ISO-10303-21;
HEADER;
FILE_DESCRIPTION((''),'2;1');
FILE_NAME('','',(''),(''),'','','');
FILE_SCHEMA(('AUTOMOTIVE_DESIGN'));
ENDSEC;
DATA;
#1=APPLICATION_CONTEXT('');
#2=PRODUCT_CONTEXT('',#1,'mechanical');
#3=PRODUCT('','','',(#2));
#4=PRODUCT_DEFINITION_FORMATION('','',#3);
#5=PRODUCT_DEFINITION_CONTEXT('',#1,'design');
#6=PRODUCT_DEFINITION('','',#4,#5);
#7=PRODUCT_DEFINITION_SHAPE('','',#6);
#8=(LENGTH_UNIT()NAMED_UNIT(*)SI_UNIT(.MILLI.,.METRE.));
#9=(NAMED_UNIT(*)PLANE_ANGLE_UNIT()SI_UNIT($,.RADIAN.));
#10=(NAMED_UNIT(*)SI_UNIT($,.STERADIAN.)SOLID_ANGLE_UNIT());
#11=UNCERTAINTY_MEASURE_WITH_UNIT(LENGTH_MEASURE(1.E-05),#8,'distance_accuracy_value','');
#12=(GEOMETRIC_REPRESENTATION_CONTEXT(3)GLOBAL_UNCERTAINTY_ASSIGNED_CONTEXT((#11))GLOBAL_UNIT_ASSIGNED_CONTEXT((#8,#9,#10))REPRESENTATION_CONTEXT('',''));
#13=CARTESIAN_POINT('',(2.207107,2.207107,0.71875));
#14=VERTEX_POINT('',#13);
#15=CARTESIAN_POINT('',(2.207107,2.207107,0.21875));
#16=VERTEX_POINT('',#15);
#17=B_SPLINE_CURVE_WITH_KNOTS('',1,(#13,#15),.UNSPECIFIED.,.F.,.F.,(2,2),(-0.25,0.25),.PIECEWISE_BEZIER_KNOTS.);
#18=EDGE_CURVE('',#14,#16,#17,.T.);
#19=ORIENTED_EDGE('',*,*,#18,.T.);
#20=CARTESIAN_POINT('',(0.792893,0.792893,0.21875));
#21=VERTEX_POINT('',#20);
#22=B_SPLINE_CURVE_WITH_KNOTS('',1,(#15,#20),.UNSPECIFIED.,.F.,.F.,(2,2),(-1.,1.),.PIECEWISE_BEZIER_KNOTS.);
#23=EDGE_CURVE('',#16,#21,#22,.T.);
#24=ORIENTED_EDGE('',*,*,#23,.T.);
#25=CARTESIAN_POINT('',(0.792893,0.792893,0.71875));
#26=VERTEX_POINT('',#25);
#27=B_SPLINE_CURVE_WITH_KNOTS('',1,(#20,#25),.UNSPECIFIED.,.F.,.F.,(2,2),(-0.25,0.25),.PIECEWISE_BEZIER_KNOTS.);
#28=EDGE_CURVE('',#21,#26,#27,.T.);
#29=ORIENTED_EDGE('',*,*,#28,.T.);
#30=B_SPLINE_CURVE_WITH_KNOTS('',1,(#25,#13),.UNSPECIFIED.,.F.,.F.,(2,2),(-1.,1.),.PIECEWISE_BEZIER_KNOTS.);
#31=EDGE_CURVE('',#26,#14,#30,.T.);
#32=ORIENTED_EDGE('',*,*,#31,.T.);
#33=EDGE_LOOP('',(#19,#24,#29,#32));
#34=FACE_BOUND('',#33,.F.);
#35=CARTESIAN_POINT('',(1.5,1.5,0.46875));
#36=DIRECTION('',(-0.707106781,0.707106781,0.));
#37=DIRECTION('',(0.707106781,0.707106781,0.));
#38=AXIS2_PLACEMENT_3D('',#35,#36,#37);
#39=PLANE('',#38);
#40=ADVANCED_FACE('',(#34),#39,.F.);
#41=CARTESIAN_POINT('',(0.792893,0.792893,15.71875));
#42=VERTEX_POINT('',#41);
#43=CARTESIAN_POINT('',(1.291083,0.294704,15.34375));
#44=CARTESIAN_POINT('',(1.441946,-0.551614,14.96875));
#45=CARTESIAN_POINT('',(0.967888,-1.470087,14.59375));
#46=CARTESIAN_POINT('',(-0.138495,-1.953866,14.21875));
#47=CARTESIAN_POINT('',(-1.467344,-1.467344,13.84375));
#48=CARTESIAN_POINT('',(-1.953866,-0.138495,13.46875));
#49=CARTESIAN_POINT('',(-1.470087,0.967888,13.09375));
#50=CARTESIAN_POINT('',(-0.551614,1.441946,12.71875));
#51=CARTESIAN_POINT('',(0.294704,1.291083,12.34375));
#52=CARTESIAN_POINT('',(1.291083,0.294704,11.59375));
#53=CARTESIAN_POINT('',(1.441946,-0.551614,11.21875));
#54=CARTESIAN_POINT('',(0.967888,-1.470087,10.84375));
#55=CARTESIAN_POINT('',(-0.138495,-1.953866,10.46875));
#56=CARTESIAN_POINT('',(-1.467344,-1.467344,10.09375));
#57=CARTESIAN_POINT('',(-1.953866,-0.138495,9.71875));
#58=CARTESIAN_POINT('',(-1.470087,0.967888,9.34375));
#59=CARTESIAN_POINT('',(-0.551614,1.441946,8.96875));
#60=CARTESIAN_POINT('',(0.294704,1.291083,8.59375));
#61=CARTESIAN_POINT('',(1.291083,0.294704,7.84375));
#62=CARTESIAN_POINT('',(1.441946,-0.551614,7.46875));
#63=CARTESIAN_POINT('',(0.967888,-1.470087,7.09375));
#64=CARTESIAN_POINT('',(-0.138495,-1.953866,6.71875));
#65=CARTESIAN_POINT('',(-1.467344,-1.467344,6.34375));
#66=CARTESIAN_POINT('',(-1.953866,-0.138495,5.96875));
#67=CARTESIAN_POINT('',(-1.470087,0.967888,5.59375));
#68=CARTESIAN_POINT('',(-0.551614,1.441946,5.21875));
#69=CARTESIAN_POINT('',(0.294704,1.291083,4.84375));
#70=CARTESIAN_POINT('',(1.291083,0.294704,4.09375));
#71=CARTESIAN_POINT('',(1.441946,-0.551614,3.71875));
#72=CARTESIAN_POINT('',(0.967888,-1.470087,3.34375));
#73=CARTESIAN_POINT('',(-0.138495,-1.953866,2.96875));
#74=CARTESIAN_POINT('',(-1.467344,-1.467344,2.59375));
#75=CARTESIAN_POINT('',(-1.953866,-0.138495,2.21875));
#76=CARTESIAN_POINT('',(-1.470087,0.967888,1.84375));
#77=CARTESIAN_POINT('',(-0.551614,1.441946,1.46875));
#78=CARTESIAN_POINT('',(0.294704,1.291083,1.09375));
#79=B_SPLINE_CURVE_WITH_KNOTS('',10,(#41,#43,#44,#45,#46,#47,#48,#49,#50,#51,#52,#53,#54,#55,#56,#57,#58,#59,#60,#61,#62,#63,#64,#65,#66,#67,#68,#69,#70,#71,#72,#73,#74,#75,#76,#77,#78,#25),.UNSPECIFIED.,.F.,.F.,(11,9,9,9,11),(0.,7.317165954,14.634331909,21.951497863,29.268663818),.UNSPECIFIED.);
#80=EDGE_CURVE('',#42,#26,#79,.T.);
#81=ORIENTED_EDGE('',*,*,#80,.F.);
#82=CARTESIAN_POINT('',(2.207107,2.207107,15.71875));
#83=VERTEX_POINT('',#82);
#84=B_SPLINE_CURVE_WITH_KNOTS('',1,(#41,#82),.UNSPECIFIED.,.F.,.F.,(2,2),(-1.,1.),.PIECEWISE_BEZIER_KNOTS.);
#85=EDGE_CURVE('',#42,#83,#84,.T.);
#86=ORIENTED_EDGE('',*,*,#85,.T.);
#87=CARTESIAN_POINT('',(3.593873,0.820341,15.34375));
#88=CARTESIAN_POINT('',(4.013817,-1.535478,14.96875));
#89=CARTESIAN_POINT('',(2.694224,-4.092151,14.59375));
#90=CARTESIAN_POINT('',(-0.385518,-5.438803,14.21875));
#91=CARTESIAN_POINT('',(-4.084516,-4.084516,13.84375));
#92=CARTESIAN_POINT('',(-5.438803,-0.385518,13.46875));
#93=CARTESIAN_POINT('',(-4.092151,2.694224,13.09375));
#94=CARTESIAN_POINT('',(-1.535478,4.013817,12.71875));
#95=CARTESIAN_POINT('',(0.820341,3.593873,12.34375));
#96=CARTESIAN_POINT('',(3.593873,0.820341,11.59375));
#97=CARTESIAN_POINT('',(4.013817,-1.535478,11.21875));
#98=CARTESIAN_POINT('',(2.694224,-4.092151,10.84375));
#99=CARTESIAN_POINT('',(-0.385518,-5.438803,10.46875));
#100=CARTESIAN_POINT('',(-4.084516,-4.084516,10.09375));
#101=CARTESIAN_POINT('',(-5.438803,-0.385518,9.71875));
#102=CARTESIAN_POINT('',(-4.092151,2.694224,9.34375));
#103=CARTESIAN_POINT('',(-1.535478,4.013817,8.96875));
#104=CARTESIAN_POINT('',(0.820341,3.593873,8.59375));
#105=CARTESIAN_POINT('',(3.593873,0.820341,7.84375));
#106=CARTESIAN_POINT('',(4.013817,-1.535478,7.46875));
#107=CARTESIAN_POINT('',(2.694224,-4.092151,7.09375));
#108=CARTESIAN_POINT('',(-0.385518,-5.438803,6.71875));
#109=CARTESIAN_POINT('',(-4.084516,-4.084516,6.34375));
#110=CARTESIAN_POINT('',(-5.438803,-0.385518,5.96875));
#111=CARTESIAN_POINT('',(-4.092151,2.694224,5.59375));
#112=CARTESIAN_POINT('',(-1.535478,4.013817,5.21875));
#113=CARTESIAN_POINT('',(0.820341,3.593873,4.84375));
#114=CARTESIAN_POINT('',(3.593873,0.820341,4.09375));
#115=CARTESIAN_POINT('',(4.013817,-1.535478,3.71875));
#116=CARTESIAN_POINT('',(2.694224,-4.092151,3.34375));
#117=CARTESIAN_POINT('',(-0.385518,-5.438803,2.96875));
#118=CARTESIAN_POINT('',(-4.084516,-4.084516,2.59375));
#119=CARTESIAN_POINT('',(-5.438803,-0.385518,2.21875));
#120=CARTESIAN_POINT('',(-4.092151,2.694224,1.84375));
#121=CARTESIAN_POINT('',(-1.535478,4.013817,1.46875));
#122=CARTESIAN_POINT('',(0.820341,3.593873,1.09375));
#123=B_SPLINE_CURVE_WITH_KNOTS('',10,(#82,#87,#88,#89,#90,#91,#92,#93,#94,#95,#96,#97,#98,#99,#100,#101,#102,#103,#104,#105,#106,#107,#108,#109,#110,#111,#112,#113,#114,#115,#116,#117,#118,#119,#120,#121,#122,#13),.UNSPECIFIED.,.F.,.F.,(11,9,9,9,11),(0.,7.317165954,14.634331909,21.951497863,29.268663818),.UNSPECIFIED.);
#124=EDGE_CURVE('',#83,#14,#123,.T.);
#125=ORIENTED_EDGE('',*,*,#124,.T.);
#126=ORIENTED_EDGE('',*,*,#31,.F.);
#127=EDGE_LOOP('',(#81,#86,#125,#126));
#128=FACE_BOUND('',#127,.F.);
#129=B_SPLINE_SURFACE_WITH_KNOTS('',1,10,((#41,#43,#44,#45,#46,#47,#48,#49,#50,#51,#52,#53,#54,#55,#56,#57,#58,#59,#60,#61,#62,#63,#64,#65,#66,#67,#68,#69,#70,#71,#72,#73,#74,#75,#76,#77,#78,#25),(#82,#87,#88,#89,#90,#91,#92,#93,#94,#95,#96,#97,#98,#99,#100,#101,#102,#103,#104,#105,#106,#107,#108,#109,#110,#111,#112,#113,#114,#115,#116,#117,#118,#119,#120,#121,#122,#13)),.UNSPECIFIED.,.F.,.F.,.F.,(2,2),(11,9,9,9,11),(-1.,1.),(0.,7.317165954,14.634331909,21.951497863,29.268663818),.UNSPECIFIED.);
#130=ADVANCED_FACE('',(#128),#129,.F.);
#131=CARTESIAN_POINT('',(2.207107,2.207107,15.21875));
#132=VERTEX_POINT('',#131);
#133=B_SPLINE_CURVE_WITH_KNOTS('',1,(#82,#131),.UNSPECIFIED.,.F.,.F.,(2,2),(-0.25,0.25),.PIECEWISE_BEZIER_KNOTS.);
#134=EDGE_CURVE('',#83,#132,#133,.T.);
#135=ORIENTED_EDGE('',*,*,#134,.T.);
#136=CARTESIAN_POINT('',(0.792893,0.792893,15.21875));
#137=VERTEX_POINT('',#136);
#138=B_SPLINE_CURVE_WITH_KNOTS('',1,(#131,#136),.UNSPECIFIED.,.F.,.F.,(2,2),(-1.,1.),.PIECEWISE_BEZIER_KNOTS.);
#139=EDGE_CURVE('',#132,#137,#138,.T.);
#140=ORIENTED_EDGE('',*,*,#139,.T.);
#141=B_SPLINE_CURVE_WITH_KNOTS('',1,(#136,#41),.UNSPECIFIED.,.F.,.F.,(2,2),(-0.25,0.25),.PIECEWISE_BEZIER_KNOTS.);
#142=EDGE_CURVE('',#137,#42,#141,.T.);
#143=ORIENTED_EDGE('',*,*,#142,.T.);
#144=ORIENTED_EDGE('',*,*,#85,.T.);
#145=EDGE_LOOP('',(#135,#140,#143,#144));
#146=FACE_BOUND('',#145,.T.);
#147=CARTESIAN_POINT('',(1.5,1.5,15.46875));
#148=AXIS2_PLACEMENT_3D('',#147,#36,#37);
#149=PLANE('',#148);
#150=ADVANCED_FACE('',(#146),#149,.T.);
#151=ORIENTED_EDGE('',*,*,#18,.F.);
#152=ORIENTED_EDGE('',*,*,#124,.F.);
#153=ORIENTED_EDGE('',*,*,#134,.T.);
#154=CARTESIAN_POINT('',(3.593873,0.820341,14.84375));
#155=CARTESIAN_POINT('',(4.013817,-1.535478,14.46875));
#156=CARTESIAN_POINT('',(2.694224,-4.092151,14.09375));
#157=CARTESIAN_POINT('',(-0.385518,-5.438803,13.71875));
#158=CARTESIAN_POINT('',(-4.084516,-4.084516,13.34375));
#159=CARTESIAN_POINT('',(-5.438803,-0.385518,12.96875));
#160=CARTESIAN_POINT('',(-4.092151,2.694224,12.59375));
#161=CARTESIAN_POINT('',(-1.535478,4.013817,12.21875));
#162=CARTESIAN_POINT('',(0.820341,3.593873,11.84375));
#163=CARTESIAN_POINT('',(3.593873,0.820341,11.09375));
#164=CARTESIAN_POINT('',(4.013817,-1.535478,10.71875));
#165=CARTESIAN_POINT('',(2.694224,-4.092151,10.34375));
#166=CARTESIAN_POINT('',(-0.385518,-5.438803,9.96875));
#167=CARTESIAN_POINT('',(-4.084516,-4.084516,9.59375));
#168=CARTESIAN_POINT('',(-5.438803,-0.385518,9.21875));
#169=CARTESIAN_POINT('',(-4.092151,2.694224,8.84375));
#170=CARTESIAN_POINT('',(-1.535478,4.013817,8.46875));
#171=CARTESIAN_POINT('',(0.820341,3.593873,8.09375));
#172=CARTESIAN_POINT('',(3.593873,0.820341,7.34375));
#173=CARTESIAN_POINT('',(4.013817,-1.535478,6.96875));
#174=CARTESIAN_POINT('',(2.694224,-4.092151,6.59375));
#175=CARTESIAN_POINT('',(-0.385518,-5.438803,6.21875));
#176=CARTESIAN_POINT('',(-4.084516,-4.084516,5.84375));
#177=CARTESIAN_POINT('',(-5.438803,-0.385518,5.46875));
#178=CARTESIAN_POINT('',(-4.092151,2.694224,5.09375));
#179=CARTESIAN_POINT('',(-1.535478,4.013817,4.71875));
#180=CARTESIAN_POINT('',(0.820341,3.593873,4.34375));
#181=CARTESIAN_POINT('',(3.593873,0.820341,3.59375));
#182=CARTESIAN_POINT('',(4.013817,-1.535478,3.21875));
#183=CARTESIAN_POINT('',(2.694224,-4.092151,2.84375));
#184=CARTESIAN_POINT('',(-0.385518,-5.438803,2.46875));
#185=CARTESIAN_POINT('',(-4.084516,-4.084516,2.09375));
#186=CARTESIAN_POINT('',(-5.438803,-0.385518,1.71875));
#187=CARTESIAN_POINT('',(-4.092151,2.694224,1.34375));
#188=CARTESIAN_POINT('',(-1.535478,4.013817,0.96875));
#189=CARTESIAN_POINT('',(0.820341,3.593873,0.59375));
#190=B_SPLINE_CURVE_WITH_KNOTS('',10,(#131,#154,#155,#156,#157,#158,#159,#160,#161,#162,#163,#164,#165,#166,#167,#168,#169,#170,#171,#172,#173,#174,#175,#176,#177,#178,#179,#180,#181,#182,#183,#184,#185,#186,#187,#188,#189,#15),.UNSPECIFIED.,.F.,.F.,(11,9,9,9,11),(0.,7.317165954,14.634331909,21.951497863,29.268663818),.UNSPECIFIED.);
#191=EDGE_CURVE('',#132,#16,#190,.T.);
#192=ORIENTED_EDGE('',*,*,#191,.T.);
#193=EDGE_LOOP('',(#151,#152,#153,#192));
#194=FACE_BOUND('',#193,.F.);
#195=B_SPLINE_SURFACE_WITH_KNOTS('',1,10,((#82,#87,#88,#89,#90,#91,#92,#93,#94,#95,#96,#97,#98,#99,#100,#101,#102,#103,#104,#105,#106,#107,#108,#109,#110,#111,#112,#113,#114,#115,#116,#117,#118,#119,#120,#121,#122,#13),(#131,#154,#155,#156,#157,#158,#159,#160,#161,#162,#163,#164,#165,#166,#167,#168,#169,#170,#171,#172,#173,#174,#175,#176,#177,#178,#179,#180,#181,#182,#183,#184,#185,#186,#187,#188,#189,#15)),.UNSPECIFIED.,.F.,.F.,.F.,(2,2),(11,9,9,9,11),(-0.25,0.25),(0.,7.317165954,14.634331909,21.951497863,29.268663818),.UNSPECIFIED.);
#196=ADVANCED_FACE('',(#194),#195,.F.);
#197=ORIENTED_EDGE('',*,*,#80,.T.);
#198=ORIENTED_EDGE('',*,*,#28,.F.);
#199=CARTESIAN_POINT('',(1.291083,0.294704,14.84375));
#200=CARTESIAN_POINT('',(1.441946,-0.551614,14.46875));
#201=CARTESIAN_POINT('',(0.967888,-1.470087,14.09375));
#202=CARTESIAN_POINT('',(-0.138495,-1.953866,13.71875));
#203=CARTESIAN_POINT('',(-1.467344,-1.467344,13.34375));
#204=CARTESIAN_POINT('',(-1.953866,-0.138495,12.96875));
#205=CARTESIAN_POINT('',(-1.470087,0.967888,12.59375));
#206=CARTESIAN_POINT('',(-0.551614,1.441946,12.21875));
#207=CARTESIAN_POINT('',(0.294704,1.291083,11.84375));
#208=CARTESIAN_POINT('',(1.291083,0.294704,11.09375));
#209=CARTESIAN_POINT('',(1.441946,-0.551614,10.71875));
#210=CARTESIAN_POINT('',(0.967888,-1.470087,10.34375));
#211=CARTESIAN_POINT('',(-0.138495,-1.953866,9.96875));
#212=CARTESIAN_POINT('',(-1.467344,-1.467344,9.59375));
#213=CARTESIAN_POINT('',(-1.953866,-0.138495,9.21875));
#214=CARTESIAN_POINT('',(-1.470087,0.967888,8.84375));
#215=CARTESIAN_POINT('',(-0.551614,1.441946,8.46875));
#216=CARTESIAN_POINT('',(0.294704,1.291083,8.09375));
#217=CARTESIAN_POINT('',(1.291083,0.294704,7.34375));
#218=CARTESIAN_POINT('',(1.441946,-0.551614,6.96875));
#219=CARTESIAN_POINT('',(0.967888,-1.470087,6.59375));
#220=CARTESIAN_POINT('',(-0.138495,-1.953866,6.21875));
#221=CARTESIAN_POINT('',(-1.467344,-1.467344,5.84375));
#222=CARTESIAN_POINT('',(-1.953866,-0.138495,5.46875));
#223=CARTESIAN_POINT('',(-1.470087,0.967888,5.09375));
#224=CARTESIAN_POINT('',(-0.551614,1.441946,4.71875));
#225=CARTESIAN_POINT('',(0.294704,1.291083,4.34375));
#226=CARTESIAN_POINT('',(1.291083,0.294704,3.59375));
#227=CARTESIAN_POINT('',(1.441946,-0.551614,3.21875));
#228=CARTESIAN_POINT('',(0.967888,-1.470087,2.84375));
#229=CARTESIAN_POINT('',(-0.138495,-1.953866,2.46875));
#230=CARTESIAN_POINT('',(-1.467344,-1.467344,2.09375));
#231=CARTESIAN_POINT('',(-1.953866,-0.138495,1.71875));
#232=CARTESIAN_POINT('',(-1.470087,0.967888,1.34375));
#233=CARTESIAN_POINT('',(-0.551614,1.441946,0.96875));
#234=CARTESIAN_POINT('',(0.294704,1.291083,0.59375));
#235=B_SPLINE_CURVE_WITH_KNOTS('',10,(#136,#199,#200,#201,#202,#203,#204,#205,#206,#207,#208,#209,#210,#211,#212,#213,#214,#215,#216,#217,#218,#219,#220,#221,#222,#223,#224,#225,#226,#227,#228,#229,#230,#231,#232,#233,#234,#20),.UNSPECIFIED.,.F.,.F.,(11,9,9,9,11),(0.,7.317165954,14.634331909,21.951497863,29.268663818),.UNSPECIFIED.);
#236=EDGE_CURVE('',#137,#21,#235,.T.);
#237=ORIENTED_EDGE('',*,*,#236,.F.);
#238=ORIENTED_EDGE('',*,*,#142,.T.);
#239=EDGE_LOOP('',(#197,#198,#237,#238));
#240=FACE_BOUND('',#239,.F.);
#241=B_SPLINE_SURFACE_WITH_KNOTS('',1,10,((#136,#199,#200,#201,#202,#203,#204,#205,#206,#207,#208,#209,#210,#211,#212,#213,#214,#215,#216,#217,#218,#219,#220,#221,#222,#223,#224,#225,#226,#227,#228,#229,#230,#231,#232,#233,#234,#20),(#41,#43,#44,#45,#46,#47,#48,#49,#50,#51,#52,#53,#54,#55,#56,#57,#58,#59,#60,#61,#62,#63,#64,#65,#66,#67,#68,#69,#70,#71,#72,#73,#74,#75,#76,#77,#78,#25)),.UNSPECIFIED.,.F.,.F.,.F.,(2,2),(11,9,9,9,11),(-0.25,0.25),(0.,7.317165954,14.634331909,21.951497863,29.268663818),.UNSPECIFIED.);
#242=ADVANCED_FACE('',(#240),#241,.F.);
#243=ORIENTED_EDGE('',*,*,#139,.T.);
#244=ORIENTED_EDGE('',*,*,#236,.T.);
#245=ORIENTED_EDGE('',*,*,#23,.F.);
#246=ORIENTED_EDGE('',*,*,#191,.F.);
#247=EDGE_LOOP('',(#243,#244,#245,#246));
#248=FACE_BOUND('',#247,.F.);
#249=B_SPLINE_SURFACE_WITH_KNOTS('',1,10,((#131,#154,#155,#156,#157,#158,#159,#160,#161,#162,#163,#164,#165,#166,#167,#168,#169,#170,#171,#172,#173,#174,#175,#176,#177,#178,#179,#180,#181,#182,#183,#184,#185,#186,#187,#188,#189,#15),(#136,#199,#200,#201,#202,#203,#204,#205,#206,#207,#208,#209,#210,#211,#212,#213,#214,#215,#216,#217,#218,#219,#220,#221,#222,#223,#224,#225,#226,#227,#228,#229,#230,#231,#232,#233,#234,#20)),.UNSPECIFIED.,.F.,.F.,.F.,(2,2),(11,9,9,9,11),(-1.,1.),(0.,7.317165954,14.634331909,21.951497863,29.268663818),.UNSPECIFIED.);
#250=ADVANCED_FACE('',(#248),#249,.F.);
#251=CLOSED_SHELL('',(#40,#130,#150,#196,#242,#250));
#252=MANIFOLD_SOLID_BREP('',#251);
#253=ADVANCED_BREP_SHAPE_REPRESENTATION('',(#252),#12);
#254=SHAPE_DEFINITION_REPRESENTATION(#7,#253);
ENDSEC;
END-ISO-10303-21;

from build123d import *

# Parameters (mm, degrees)
SWEEP1_PITCH       = 3.75
SWEEP1_HEIGHT      = 15
SWEEP1_RADIUS      = 3
SWEEP1_START_ANGLE = 135
SKETCH16_W         = 2
SKETCH16_H         = 0.5


with BuildPart() as part:
    # Sweep1: sweep along a helix
    with BuildLine() as sweep1_path:
        add(Helix(SWEEP1_PITCH, SWEEP1_HEIGHT, SWEEP1_RADIUS, center=(0, 0, 15), direction=(0, 0, -1), mode=Mode.PRIVATE).rotate(Axis((0, 0, 15), (0, 0, -1)), SWEEP1_START_ANGLE))
    # Sketch16 → Sweep1 (sweep)
    with BuildSketch(Plane(origin=(0, 0, 0), x_dir=(1, 0, 0), z_dir=(0, 1, 0))):
        with Locations((2.121320344, -15)):
            Rectangle(SKETCH16_W, SKETCH16_H)
    sweep(path=sweep1_path.line, is_frenet=True)


solid = part.part
